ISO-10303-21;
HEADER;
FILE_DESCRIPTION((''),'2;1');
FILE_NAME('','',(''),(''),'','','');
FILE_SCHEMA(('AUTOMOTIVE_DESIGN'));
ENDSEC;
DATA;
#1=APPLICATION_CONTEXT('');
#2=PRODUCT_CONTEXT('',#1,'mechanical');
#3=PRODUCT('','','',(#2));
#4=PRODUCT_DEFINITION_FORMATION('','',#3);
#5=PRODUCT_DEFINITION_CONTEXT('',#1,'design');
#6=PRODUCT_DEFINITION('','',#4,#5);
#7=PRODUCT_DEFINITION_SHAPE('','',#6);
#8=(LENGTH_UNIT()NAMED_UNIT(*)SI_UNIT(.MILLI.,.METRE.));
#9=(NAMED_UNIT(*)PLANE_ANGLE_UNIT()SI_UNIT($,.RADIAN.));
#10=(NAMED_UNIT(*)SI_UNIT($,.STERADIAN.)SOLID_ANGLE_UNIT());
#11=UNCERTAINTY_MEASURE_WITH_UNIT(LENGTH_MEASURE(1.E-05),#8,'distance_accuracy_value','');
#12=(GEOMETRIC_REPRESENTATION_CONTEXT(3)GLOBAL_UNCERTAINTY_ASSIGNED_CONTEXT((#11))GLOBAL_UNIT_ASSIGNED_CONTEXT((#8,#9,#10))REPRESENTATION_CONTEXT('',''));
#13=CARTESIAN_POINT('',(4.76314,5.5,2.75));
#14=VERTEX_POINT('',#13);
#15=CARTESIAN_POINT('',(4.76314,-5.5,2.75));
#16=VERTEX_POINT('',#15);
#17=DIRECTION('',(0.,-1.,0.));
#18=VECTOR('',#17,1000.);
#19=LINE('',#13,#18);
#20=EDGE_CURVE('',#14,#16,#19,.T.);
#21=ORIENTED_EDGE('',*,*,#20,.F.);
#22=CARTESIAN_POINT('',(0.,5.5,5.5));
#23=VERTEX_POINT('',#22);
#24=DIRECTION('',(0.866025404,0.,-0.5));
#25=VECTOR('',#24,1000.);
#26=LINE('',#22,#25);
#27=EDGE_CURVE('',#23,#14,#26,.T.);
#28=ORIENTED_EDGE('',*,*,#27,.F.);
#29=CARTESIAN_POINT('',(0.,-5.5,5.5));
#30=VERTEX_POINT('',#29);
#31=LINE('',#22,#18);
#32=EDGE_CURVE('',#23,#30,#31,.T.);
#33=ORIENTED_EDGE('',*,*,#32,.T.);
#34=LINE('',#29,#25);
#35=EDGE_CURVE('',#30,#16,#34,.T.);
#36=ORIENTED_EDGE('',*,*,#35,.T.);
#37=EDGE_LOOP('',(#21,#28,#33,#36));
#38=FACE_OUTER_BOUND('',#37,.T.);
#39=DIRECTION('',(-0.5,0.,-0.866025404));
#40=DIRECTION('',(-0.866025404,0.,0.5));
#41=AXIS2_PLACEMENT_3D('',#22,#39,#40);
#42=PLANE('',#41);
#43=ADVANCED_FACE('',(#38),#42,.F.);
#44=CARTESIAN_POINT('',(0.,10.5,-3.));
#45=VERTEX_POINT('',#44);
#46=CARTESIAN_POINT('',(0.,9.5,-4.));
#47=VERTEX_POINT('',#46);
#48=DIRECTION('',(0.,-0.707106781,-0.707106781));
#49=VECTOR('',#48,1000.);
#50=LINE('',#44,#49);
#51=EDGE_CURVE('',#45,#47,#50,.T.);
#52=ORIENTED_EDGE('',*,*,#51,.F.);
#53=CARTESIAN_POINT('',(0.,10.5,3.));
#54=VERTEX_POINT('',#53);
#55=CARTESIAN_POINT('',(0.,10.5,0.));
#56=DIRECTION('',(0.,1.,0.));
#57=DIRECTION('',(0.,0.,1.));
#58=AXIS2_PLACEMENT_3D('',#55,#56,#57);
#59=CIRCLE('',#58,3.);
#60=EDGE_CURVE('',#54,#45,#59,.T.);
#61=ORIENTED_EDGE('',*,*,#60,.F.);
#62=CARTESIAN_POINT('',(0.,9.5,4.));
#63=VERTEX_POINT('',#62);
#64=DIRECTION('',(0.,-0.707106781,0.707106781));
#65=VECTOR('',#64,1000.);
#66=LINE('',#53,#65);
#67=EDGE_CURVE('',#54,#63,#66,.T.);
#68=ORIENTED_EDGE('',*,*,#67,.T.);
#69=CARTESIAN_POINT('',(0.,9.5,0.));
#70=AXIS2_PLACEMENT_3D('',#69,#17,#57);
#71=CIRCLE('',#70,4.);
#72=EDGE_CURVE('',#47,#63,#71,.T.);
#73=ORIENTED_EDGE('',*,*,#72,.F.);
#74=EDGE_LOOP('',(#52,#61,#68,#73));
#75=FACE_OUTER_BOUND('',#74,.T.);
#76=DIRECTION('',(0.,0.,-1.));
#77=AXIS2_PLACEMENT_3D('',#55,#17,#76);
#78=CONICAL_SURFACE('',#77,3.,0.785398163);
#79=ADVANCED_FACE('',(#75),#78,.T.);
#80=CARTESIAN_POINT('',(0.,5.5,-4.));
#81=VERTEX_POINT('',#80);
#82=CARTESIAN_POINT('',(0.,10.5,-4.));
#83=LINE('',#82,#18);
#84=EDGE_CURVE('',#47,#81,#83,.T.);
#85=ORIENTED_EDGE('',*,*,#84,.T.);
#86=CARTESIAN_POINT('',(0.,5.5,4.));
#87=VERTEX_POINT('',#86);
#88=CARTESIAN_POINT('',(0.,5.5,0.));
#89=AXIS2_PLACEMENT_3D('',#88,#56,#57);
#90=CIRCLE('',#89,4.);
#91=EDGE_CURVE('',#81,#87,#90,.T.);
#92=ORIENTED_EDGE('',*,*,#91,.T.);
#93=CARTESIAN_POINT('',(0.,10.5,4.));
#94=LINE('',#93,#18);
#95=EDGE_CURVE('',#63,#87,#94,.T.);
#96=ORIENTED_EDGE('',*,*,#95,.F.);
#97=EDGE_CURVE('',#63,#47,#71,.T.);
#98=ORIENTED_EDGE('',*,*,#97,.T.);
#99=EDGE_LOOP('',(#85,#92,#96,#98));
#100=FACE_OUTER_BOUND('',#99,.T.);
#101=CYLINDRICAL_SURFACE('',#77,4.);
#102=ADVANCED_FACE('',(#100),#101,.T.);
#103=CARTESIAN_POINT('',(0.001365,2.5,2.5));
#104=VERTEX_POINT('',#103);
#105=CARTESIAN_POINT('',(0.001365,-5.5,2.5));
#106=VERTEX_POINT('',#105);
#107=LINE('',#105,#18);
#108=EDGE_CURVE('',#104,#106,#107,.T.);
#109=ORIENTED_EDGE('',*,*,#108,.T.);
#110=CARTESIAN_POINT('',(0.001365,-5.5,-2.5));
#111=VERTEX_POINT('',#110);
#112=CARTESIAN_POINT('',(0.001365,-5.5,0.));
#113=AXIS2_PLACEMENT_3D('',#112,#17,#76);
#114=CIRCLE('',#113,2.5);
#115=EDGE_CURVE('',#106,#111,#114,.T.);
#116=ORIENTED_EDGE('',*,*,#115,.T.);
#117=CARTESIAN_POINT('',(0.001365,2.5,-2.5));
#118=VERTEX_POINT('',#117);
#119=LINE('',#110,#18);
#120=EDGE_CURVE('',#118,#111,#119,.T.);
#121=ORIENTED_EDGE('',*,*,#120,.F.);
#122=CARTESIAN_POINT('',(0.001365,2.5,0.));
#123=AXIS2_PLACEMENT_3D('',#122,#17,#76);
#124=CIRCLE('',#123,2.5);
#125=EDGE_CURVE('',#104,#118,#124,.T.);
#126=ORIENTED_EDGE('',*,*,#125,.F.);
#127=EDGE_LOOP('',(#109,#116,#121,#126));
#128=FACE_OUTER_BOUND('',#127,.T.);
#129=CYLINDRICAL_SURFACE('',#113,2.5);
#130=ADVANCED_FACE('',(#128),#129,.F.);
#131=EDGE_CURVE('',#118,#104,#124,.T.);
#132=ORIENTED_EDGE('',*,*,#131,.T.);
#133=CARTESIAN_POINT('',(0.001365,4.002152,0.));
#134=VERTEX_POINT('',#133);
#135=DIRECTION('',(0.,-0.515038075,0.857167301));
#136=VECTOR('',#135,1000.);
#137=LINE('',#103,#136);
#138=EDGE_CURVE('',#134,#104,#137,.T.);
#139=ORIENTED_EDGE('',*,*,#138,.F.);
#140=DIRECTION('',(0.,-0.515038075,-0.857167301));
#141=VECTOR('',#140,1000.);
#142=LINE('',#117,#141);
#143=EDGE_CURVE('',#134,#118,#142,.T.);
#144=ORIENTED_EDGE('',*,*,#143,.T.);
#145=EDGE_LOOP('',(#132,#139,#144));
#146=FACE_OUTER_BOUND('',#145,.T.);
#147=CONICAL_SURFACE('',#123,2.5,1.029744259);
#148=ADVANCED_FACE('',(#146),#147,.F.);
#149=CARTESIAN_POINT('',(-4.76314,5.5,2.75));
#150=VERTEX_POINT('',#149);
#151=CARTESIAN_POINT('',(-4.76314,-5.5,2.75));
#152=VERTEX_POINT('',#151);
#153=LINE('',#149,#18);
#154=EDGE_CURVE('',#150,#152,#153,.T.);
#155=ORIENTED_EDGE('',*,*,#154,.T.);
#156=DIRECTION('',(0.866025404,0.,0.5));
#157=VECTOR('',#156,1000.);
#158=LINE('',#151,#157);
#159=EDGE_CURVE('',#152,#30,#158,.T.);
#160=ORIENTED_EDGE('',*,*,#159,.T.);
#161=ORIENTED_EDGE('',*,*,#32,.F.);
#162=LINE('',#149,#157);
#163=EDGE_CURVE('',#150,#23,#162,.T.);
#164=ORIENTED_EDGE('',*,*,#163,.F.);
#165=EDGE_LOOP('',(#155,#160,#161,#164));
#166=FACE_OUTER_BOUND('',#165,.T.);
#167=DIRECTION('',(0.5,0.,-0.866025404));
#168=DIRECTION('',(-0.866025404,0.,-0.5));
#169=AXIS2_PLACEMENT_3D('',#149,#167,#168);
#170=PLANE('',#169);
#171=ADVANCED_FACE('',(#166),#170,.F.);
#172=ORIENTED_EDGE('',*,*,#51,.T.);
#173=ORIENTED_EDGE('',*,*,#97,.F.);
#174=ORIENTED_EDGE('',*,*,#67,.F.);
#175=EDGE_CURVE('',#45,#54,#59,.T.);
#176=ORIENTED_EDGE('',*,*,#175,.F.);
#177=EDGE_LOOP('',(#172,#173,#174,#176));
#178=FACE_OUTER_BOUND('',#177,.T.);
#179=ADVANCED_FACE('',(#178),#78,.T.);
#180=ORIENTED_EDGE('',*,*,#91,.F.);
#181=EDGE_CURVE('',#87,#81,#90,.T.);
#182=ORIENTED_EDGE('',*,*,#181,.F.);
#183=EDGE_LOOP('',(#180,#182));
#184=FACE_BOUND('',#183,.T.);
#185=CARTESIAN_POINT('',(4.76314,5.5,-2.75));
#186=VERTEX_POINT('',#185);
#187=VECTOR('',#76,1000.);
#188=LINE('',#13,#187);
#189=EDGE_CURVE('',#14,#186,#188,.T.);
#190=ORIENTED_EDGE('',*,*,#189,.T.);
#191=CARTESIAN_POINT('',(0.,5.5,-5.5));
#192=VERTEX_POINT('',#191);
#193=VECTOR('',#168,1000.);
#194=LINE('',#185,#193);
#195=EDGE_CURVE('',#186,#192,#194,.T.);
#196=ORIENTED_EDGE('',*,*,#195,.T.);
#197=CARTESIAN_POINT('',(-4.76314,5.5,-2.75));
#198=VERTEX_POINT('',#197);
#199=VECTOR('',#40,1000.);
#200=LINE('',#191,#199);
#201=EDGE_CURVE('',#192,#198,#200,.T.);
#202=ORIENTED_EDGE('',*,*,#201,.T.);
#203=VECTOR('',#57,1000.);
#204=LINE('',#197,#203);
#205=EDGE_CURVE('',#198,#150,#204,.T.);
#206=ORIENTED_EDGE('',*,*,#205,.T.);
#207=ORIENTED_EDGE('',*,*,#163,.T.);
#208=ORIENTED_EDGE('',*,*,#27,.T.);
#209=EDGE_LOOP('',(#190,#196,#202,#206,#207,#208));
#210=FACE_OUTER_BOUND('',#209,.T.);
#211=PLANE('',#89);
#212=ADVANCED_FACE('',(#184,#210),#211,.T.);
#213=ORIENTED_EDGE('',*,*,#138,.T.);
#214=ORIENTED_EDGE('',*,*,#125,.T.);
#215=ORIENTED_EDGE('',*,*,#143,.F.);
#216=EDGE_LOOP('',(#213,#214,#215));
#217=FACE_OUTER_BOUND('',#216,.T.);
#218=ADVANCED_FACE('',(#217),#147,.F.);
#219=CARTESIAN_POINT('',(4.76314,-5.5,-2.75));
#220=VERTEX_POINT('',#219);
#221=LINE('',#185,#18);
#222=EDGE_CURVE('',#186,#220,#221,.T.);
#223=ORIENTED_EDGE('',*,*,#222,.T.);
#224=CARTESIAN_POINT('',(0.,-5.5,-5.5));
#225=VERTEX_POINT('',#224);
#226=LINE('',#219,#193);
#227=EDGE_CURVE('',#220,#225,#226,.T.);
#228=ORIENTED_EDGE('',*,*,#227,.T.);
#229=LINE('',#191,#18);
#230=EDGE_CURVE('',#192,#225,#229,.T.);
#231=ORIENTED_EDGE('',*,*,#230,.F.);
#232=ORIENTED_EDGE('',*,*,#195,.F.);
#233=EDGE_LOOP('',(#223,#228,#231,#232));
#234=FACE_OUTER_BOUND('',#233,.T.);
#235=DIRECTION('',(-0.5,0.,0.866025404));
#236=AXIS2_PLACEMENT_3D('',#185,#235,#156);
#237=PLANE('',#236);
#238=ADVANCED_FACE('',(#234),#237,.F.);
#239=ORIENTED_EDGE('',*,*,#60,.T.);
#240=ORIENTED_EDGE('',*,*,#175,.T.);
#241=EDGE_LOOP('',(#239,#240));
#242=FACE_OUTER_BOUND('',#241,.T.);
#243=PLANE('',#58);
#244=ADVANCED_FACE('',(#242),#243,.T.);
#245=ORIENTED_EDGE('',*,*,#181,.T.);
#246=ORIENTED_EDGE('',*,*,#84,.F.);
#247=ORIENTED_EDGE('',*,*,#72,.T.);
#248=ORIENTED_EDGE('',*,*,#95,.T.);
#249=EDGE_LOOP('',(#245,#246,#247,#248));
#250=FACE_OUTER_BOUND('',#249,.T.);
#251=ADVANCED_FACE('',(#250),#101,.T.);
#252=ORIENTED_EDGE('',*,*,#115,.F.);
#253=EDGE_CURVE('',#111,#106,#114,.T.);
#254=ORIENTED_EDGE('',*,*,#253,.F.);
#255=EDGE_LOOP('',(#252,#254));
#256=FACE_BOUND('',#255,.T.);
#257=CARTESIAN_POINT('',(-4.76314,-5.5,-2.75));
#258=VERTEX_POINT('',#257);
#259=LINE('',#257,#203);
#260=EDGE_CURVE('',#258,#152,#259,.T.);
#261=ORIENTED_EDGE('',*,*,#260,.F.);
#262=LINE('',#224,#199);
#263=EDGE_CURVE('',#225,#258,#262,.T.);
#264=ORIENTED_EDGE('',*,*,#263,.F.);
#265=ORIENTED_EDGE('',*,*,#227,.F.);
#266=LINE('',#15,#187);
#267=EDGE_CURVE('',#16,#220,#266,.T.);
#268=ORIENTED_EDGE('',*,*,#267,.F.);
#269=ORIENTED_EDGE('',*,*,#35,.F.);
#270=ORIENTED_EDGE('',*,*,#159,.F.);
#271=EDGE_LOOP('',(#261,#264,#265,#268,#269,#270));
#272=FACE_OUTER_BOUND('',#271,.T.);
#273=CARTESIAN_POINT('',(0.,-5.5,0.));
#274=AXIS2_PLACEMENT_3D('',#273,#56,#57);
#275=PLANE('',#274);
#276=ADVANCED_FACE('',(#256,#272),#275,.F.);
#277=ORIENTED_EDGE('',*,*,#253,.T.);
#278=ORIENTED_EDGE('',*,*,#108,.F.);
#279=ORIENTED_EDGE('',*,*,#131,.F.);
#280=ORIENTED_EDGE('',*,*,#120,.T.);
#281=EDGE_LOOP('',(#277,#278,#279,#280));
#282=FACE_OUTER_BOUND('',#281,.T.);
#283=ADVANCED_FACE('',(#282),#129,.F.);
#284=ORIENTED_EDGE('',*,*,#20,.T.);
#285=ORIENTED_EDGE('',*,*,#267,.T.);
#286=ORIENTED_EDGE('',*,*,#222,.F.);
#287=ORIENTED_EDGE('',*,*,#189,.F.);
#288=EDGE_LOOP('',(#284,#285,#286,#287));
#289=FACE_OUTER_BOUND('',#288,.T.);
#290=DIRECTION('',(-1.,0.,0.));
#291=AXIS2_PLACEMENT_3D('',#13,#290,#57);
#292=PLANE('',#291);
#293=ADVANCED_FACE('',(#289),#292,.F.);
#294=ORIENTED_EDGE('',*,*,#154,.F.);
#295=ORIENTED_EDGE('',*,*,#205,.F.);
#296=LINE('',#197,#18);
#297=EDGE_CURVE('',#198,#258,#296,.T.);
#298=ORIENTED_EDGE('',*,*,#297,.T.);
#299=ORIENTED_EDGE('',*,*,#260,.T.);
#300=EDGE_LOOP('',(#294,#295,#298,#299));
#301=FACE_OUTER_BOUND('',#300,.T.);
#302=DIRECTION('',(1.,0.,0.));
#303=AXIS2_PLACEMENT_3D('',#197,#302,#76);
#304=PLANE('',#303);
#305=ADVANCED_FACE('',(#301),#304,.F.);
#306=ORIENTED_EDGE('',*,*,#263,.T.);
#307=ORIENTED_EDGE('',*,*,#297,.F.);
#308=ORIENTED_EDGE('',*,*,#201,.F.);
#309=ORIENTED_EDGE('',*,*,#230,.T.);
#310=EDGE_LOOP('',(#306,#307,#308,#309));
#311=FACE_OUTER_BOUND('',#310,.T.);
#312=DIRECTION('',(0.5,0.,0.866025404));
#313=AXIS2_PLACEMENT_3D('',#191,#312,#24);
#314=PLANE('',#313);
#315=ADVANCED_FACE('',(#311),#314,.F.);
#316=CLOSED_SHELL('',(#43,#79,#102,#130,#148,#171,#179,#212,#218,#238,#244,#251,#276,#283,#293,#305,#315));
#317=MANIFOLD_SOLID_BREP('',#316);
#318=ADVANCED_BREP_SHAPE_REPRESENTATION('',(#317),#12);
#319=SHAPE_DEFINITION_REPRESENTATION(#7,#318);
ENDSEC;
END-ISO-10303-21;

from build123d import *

# Parameters (mm, degrees)
BOSS_EXTRUDE1_DEPTH       = 5.5
SKETCH3_R                 = 4
BOSS_EXTRUDE2_DEPTH       = 5
CHAMFER1_SIZE             = 1
M6X1_0_TAPPED_HOLE1_D     = 5
M6X1_0_TAPPED_HOLE1_DEPTH = 8
M6X1_0_TAPPED_HOLE1_TIP   = 1.502151548


with BuildPart() as part:
    # Sketch1 → Boss-Extrude1 (new, symmetric)
    with BuildSketch(Plane(origin=(0, 0, 0), x_dir=(1, 0, 0), z_dir=(0, 1, 0))):
        Polygon((0, 5.5), (-4.763139721, 2.75), (-4.763139721, -2.75), (0, -5.5), (4.763139721, -2.75), (4.763139721, 2.75), align=None)
    extrude(amount=BOSS_EXTRUDE1_DEPTH, both=True)

    # Sketch3 → Boss-Extrude2 (add)
    with BuildSketch(Plane(origin=(0, 5.5, 0), x_dir=(1, 0, 0), z_dir=(0, 1, 0))):
        with Locations(Location((0, 0, 0), (0, 0, 270))):
            Circle(SKETCH3_R)
    extrude(amount=BOSS_EXTRUDE2_DEPTH)

    # Chamfer1
    chamfer1_edges = [part.edges().sort_by_distance(p)[0] for p in [
        (0, 10.5, -4),
    ]]
    chamfer(chamfer1_edges, length=CHAMFER1_SIZE)

    # M6x1.0 Tapped Hole1
    with Locations(Plane(origin=(0, -5.5, 0), x_dir=(-1, 0, 0), z_dir=(0, -1, 0))):
        with Locations((-0.001364709, 0)):
            Hole(M6X1_0_TAPPED_HOLE1_D / 2, depth=M6X1_0_TAPPED_HOLE1_DEPTH)
            with Locations((0, 0, -(M6X1_0_TAPPED_HOLE1_DEPTH + M6X1_0_TAPPED_HOLE1_TIP / 2))):  # 118° drill point
                Cone(0, M6X1_0_TAPPED_HOLE1_D / 2, M6X1_0_TAPPED_HOLE1_TIP, mode=Mode.SUBTRACT)


solid = part.part
